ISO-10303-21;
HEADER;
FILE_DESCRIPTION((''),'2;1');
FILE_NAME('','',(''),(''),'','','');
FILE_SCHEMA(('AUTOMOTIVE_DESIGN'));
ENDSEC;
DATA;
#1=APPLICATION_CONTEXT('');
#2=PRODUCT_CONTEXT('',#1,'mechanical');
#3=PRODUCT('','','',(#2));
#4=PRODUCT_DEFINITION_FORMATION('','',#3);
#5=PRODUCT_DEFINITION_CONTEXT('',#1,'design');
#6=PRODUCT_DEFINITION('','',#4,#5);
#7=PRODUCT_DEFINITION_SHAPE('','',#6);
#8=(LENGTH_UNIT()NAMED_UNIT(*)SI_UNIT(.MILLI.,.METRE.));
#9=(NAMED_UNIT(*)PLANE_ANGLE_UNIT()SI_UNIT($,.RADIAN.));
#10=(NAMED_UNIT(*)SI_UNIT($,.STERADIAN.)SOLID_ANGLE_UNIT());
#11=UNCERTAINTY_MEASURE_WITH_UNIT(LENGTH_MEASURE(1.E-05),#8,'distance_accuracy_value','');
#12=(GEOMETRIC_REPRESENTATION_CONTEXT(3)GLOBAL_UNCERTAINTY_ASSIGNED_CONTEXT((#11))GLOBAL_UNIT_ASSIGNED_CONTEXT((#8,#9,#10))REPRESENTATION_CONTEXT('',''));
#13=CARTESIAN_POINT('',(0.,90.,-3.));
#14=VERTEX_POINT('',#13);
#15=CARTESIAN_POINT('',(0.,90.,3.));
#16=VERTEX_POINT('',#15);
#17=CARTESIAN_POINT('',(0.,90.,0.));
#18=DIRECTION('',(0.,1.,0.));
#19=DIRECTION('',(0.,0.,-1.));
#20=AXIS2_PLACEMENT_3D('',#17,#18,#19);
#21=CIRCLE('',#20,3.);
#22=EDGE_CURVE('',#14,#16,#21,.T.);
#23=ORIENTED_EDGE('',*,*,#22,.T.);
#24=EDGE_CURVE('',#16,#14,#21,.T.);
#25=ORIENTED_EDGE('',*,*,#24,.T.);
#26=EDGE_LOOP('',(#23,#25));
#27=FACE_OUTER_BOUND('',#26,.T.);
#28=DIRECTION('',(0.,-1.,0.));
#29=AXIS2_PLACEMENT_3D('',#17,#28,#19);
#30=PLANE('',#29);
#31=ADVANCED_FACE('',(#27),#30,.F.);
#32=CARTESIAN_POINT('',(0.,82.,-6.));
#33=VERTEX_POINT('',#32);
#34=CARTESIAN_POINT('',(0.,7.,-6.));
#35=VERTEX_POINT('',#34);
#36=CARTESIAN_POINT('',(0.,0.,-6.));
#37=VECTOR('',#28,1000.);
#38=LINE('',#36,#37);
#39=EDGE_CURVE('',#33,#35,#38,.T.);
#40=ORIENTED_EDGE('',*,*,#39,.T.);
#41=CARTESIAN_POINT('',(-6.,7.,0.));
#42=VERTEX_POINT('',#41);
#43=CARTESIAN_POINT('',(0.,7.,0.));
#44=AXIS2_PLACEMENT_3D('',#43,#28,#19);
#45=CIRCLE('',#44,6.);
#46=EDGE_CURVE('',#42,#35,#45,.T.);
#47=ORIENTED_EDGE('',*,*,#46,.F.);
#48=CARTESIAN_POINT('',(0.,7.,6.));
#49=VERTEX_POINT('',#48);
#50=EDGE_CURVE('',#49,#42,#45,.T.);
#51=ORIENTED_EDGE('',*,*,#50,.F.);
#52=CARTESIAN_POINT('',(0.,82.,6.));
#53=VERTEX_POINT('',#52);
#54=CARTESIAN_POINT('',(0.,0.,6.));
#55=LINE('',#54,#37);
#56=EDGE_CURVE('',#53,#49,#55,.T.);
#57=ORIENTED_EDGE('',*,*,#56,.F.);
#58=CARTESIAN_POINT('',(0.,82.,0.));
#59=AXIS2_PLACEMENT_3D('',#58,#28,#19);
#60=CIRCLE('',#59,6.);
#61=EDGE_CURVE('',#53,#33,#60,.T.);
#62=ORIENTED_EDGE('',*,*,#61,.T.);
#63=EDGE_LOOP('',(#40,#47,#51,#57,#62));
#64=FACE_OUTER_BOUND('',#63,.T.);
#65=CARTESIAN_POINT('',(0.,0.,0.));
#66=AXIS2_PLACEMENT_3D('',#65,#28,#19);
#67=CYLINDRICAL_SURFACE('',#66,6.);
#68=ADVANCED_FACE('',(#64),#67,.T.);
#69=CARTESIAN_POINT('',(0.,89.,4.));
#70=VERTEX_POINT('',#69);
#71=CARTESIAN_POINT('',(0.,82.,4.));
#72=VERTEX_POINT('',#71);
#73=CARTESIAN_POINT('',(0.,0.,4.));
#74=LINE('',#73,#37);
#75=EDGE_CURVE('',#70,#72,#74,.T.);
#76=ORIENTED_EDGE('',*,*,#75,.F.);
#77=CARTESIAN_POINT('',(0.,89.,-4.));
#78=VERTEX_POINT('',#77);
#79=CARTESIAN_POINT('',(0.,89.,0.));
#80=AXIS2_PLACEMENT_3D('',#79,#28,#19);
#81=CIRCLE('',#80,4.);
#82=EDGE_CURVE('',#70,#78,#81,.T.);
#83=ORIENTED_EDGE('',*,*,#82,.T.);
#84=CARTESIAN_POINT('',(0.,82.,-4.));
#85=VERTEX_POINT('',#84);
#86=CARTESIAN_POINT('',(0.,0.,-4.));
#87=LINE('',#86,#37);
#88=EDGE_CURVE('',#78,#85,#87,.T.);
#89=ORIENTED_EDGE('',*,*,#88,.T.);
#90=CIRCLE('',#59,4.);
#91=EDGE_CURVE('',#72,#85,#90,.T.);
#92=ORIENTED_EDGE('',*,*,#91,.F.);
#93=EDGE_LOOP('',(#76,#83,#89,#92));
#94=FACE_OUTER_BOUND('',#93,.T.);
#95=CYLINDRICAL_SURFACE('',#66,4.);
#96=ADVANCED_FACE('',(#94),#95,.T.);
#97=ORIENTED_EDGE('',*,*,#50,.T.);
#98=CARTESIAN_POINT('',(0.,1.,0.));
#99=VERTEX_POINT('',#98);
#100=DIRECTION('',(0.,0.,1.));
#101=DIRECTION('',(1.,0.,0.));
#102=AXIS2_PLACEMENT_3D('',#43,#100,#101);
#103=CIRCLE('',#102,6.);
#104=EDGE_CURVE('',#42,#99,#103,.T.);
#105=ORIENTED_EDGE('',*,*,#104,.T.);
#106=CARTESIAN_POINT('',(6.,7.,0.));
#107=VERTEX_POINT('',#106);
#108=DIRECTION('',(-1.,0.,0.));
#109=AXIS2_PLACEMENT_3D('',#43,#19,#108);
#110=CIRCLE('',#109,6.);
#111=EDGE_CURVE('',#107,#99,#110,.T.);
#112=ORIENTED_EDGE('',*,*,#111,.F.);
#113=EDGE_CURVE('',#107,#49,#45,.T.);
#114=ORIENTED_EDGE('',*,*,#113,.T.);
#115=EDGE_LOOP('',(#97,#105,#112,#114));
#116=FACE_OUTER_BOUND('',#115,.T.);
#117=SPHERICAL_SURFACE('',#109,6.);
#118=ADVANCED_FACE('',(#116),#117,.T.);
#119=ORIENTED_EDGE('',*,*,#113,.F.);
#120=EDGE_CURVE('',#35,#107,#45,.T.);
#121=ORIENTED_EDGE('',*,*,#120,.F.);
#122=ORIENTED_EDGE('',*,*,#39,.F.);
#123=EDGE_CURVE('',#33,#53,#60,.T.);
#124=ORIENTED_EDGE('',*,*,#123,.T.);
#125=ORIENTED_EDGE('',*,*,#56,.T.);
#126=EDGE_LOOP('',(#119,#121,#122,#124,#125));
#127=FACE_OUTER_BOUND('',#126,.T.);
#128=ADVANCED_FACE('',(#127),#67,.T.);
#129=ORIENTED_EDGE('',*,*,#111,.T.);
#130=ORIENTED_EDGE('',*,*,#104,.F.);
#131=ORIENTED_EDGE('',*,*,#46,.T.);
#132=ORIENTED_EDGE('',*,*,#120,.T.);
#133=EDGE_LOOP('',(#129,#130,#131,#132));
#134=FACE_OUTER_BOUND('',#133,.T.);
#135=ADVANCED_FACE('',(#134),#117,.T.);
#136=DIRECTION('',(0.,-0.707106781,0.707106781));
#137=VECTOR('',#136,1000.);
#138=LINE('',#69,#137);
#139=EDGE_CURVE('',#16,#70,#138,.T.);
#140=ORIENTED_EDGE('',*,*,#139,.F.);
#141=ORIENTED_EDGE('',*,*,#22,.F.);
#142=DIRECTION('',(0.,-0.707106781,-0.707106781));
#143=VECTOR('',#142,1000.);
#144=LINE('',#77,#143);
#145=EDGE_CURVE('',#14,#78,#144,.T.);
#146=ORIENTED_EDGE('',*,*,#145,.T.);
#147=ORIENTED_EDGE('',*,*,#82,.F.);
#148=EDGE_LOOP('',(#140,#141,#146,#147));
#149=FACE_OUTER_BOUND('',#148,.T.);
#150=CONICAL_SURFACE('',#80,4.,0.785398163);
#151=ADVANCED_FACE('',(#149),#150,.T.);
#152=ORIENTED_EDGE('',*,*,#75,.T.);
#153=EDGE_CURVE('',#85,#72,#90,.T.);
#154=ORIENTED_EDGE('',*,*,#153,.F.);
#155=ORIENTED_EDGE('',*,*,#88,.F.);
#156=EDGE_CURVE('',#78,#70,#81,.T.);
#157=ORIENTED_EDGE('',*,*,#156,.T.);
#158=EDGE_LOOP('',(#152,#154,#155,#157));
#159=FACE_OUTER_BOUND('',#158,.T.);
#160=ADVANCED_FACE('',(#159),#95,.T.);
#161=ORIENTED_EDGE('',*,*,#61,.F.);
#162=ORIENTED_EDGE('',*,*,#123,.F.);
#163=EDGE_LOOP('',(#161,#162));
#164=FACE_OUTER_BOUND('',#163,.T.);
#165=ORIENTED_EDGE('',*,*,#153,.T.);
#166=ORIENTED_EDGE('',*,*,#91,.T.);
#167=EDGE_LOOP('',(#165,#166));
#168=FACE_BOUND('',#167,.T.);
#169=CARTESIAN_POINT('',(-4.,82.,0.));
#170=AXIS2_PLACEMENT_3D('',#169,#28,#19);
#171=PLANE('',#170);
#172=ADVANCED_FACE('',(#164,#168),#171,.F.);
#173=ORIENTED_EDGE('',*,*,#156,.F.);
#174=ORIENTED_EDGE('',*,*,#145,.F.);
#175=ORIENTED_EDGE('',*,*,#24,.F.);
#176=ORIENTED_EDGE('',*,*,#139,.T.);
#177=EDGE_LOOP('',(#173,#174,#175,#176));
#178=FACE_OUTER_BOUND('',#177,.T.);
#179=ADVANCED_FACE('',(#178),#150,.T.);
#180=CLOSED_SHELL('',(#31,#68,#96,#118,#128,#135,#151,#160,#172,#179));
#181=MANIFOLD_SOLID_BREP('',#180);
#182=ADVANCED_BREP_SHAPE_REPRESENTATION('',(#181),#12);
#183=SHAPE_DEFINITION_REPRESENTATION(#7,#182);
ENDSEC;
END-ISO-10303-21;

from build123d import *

# Parameters (mm, degrees)
CHAMFER1_SIZE = 1


with BuildPart() as part:
    # Sketch1 → Revolve1 (revolve)
    with BuildSketch(Plane.XY, mode=Mode.PRIVATE) as revolve1_sk:
        with BuildLine():
            Line((0, 90), (-4, 90))
            Line((-4, 90), (-4, 82))
            Line((-4, 82), (-6, 82))
            Line((-6, 82), (-6, 7))
            ThreePointArc((-6, 7), (-4.242640687, 2.757359313), (0, 1))
            Line((0, 1), (0, 90))
        make_face()
    revolve(revolve1_sk.sketch.rotate(Axis((0, 0, 0), (0, 1, 0)), 270), axis=Axis((0, 0, 0), (0, 1, 0)))

    # Chamfer1
    chamfer1_edges = [part.edges().sort_by_distance(p)[0] for p in [
        (0, 90, 4),
    ]]
    chamfer(chamfer1_edges, length=CHAMFER1_SIZE)


solid = part.part
